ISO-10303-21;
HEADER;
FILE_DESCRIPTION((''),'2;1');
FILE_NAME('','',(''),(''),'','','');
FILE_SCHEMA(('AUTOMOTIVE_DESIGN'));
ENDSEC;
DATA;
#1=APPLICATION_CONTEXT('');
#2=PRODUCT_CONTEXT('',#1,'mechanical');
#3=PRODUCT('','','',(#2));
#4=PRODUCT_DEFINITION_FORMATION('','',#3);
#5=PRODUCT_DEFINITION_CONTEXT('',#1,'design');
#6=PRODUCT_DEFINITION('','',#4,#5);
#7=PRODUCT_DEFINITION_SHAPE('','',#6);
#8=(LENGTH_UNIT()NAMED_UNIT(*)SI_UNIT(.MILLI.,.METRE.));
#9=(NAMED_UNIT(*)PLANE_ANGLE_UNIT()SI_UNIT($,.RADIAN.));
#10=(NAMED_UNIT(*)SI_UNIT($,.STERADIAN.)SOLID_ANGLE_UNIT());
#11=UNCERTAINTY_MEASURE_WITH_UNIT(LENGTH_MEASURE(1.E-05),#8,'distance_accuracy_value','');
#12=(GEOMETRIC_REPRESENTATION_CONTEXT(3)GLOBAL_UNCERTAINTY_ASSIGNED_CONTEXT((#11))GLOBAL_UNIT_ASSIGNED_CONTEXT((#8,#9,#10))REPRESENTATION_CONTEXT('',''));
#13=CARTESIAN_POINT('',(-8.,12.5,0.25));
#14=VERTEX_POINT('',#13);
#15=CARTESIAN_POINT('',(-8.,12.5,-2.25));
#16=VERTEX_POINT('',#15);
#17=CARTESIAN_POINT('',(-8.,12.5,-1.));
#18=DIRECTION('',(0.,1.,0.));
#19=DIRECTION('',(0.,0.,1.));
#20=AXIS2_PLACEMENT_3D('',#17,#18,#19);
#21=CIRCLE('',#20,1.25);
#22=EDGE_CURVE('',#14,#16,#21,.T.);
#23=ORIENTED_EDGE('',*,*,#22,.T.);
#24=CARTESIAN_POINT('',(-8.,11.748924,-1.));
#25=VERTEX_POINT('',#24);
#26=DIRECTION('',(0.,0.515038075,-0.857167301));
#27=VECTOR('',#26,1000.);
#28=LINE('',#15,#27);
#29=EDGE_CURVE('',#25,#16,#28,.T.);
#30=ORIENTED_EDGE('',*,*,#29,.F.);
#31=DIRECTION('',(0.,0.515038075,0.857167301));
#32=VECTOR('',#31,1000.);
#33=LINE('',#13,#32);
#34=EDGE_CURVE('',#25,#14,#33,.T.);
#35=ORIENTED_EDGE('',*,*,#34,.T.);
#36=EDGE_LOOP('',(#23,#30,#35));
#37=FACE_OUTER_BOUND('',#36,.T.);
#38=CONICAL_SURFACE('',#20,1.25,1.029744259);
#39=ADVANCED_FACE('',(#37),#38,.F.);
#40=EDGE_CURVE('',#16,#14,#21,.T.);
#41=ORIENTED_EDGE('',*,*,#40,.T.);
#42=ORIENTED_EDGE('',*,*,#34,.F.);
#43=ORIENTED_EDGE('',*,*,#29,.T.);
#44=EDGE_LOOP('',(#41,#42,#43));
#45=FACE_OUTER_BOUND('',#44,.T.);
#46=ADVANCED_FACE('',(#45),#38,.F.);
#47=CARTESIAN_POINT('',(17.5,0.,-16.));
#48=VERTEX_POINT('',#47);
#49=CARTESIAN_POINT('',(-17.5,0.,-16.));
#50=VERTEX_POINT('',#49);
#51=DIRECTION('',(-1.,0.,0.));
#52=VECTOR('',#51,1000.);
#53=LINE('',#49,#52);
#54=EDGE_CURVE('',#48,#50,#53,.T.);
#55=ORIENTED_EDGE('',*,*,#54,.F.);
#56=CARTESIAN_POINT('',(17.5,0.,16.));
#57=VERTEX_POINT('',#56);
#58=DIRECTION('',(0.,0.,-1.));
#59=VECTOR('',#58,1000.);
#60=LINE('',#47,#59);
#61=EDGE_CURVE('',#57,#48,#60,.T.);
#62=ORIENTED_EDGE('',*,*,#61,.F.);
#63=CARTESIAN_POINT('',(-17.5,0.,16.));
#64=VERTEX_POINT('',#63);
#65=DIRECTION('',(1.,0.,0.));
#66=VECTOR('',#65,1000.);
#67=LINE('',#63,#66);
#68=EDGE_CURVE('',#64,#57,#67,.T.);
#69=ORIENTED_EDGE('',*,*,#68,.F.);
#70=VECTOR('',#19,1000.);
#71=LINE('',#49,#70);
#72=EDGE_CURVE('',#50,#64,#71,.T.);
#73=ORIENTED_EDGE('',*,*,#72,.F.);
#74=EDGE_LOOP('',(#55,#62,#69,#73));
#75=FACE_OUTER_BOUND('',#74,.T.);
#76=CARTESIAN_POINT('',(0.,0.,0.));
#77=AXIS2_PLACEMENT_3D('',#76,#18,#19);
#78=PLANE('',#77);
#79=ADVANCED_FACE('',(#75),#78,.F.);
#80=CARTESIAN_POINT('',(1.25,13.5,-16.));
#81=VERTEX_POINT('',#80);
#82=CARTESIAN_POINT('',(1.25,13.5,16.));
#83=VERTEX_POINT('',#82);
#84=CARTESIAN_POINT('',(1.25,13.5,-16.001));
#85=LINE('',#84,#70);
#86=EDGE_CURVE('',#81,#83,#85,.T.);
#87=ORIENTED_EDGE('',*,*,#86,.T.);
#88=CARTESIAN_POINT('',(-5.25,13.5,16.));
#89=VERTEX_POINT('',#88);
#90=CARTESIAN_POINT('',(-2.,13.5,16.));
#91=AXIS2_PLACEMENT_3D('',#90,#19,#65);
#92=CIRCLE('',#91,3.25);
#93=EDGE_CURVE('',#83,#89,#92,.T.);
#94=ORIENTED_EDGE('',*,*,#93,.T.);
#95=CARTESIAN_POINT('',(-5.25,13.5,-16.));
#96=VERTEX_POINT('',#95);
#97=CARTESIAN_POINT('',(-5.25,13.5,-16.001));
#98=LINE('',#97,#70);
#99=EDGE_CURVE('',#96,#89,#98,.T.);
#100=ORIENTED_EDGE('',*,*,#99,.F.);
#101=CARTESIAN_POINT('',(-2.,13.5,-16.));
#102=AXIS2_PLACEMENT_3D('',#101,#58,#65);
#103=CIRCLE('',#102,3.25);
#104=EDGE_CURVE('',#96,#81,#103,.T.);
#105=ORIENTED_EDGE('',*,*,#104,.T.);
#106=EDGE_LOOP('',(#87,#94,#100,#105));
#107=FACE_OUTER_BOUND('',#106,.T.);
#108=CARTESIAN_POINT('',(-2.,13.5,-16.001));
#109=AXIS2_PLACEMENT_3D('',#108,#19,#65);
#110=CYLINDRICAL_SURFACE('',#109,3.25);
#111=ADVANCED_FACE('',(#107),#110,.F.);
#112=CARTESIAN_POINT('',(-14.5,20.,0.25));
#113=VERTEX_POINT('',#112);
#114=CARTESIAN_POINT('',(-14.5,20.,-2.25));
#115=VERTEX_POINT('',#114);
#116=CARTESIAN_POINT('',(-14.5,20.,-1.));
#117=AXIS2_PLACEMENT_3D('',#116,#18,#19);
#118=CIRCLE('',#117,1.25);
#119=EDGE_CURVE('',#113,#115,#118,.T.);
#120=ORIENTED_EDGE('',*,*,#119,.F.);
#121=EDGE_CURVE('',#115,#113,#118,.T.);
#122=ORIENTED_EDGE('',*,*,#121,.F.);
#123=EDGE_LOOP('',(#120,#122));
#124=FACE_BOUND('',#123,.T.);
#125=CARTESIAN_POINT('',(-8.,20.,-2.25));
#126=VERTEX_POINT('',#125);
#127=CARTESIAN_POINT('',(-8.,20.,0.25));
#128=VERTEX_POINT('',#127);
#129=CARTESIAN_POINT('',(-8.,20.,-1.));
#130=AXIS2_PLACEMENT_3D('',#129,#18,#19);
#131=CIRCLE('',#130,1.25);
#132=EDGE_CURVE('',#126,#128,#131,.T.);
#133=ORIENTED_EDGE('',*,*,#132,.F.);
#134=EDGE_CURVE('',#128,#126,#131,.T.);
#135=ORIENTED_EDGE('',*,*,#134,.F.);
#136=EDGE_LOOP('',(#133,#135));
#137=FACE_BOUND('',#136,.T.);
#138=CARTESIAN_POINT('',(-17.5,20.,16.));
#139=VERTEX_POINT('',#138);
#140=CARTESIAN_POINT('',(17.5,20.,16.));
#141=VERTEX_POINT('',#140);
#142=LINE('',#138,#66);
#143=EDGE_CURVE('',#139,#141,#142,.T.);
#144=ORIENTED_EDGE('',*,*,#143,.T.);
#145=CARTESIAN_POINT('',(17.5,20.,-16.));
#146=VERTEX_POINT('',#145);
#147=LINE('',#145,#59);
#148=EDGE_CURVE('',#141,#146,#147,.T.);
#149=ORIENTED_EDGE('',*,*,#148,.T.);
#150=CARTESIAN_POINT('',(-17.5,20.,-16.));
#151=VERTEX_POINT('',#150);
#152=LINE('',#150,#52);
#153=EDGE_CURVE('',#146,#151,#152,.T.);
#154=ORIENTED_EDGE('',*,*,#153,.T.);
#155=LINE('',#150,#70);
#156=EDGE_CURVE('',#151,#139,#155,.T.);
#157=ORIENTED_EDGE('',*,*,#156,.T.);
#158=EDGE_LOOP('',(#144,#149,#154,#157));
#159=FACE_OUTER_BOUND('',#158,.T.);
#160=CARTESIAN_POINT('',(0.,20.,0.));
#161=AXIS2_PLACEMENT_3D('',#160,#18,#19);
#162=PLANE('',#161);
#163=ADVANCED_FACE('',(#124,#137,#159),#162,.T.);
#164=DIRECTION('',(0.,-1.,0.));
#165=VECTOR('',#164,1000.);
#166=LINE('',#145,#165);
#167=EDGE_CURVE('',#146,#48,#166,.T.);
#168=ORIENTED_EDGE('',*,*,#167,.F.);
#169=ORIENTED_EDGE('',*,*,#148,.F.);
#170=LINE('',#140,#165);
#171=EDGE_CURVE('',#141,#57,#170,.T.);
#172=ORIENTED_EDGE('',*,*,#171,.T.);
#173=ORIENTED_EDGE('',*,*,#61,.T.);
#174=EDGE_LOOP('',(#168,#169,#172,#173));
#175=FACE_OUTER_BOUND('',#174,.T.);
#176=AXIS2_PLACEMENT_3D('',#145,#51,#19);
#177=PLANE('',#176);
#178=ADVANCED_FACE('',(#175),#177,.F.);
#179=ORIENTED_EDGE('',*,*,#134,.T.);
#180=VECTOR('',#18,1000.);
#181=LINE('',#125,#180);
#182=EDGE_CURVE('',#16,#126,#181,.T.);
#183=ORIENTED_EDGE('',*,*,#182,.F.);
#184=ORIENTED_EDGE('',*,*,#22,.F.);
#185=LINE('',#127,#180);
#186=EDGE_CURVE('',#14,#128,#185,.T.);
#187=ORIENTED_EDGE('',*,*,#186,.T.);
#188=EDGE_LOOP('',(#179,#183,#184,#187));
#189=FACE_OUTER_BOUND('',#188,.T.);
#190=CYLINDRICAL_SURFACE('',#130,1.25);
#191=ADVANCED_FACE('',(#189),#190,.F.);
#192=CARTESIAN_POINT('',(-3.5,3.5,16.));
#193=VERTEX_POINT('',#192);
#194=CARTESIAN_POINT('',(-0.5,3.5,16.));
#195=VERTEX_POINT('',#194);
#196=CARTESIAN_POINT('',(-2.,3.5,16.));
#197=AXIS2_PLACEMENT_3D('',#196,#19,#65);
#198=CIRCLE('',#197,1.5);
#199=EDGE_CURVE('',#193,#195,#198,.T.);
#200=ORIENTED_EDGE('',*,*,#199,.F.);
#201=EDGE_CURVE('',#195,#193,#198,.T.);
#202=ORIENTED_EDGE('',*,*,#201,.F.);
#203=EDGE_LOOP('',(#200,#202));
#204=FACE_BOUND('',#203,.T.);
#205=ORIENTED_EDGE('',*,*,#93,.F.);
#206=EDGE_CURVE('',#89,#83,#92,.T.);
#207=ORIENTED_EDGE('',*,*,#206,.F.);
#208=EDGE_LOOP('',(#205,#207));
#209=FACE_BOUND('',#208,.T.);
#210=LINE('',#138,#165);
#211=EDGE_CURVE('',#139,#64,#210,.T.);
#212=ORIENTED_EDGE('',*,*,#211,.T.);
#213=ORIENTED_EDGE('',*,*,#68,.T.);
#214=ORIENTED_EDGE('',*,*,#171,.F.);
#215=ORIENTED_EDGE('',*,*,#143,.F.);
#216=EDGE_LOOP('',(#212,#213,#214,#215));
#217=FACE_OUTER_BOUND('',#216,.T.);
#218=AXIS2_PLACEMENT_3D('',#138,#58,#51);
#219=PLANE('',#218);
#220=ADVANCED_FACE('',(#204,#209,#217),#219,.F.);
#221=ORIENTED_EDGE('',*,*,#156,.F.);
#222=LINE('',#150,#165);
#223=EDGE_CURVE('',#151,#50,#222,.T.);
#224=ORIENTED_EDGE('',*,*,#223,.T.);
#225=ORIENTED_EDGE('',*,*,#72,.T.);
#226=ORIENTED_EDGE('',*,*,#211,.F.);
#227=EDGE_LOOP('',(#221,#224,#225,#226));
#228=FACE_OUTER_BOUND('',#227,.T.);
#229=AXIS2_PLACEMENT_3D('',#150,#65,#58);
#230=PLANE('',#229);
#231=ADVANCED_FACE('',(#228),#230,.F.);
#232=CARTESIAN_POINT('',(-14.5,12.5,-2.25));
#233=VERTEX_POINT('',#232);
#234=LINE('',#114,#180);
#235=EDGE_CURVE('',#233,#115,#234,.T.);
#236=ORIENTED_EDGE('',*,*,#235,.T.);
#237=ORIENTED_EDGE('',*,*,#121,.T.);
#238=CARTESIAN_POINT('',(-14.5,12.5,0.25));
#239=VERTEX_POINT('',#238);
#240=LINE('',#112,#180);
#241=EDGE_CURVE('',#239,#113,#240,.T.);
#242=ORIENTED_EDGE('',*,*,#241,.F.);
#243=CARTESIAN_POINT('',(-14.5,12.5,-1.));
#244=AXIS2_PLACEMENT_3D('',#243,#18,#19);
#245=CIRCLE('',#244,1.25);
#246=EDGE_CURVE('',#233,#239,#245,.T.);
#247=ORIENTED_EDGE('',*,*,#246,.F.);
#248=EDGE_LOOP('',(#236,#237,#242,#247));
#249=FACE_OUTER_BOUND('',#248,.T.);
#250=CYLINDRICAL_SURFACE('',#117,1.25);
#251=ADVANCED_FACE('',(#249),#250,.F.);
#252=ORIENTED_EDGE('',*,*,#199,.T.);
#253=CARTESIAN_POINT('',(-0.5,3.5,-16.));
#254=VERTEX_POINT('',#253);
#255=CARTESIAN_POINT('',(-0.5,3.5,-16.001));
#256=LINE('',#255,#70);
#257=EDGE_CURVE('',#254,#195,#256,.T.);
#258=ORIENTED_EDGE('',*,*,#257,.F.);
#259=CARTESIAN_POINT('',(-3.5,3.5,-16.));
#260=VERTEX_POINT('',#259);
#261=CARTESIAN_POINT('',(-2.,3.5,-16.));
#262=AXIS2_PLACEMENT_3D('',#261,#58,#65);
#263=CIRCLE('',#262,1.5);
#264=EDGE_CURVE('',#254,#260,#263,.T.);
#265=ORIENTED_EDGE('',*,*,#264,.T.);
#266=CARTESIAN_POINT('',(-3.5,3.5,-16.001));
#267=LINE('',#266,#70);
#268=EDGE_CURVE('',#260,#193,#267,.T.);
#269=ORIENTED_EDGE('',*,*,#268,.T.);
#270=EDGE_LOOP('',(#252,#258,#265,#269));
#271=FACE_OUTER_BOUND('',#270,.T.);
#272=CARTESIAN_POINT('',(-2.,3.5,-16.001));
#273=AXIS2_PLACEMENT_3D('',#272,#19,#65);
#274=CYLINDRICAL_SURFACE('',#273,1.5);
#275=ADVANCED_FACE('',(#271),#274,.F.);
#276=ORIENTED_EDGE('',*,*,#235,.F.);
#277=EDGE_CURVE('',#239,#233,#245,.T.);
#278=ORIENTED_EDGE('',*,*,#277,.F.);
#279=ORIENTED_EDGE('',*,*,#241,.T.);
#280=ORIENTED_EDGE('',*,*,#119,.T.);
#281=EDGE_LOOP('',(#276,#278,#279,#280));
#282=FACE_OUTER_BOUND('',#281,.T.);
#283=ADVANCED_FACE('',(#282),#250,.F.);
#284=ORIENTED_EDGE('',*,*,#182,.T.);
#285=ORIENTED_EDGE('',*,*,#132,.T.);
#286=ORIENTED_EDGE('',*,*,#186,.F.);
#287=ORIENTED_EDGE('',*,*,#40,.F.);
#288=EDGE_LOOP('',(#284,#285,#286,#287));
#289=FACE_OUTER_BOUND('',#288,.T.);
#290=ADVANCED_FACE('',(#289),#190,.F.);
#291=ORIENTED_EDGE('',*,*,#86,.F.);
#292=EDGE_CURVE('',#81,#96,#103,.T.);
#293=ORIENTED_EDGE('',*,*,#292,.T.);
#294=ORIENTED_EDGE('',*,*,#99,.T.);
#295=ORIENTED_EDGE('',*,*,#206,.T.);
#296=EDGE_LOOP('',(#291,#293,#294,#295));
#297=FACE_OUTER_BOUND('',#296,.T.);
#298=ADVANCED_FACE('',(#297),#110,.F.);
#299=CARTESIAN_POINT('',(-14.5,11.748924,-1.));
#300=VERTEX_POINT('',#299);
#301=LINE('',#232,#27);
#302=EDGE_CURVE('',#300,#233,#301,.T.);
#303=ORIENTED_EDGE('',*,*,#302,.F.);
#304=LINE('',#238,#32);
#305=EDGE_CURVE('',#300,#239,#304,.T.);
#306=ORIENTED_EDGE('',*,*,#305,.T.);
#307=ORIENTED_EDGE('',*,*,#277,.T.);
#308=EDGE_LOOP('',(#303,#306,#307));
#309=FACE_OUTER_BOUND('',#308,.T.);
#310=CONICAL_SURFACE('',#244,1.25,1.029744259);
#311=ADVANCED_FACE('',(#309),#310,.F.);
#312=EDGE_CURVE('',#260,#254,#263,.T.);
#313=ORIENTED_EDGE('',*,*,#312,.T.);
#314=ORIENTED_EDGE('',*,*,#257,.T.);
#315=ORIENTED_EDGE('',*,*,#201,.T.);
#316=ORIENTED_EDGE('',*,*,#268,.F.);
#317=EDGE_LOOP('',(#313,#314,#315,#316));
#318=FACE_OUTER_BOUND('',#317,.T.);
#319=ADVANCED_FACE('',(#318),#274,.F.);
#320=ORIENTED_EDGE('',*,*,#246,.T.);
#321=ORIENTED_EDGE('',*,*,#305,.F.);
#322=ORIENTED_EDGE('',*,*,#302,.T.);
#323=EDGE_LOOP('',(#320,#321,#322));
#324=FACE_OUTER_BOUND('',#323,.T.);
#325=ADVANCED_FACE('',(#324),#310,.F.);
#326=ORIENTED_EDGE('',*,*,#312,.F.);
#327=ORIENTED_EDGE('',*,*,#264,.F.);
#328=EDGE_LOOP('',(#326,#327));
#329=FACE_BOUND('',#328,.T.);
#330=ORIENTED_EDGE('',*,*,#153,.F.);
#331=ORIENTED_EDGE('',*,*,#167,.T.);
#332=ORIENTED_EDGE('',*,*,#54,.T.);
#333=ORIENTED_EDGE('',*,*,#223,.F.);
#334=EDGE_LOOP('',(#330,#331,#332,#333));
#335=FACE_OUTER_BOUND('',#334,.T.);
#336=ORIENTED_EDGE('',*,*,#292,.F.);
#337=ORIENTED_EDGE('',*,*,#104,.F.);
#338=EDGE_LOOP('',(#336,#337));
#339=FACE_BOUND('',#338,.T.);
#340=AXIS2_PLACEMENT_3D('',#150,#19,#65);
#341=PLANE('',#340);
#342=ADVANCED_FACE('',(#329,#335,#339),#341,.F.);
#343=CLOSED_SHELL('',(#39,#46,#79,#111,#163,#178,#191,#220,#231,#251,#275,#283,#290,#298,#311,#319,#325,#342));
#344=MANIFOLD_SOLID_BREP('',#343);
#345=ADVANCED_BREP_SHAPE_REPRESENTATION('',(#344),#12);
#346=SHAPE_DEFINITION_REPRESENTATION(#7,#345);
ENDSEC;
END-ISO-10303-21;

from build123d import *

# Parameters (mm, degrees)
SKETCH1_W             = 35
SKETCH1_H             = 32
BOSS_EXTRUDE1_DEPTH   = 20
CUT_EXTRUDE2_REACH    = 43.596
SKETCH3_R             = 3.25
SKETCH3_R_2           = 1.5
SKETCH4_R             = 1
CUT_EXTRUDE3_DEPTH    = 2
M3_TAPPED_HOLE1_D     = 2.5
M3_TAPPED_HOLE1_DEPTH = 7.5
M3_TAPPED_HOLE1_TIP   = 0.751075774


with BuildPart() as part:
    # Sketch1 → Boss-Extrude1 (new body)
    with BuildSketch(Plane(origin=(0, 0, 0), x_dir=(1, 0, 0), z_dir=(0, 1, 0))):
        Rectangle(SKETCH1_W, SKETCH1_H)
    extrude(amount=BOSS_EXTRUDE1_DEPTH)

    # Sketch3 → Cut-Extrude2 (cut, up to next)
    with BuildSketch(Plane.XY.offset(16), mode=Mode.PRIVATE) as cut_extrude2_sk1:
        with Locations((-2, 13.5)):
            Circle(SKETCH3_R)
    cut_extrude2_tool1 = extrude(cut_extrude2_sk1.sketch, amount=-CUT_EXTRUDE2_REACH, mode=Mode.PRIVATE) & part.part
    # Sketch3 → Cut-Extrude2 (cut, up to next)
    with BuildSketch(Plane.XY.offset(16), mode=Mode.PRIVATE) as cut_extrude2_sk2:
        with Locations((-2, 3.5)):
            Circle(SKETCH3_R_2)
    cut_extrude2_tool2 = extrude(cut_extrude2_sk2.sketch, amount=-CUT_EXTRUDE2_REACH, mode=Mode.PRIVATE) & part.part
    add(cut_extrude2_tool1.solids().sort_by_distance((-2, 13.5, 16))[0], mode=Mode.SUBTRACT)
    add(cut_extrude2_tool2.solids().sort_by_distance((-2, 3.5, 16))[0], mode=Mode.SUBTRACT)

    # Sketch4 → Cut-Extrude3 (cut)
    with BuildSketch(Plane(origin=(0, 20, 0), x_dir=(1, 0, 0), z_dir=(0, 1, 0))):
        with Locations(Location((-8, 1, 0), (0, 0, 270))):
            Circle(SKETCH4_R)
        with Locations(Location((-14.5, 1, 0), (0, 0, 270))):
            Circle(SKETCH4_R)
    extrude(amount=-CUT_EXTRUDE3_DEPTH, mode=Mode.SUBTRACT)

    # M3 Tapped Hole1
    with Locations(Plane(origin=(0, 20, 0), x_dir=(1, 0, 0), z_dir=(0, 1, 0))):
        with Locations((-8, 1), (-14.5, 1)):
            Hole(M3_TAPPED_HOLE1_D / 2, depth=M3_TAPPED_HOLE1_DEPTH)
            with Locations((0, 0, -(M3_TAPPED_HOLE1_DEPTH + M3_TAPPED_HOLE1_TIP / 2))):  # 118° drill point
                Cone(0, M3_TAPPED_HOLE1_D / 2, M3_TAPPED_HOLE1_TIP, mode=Mode.SUBTRACT)


solid = part.part
